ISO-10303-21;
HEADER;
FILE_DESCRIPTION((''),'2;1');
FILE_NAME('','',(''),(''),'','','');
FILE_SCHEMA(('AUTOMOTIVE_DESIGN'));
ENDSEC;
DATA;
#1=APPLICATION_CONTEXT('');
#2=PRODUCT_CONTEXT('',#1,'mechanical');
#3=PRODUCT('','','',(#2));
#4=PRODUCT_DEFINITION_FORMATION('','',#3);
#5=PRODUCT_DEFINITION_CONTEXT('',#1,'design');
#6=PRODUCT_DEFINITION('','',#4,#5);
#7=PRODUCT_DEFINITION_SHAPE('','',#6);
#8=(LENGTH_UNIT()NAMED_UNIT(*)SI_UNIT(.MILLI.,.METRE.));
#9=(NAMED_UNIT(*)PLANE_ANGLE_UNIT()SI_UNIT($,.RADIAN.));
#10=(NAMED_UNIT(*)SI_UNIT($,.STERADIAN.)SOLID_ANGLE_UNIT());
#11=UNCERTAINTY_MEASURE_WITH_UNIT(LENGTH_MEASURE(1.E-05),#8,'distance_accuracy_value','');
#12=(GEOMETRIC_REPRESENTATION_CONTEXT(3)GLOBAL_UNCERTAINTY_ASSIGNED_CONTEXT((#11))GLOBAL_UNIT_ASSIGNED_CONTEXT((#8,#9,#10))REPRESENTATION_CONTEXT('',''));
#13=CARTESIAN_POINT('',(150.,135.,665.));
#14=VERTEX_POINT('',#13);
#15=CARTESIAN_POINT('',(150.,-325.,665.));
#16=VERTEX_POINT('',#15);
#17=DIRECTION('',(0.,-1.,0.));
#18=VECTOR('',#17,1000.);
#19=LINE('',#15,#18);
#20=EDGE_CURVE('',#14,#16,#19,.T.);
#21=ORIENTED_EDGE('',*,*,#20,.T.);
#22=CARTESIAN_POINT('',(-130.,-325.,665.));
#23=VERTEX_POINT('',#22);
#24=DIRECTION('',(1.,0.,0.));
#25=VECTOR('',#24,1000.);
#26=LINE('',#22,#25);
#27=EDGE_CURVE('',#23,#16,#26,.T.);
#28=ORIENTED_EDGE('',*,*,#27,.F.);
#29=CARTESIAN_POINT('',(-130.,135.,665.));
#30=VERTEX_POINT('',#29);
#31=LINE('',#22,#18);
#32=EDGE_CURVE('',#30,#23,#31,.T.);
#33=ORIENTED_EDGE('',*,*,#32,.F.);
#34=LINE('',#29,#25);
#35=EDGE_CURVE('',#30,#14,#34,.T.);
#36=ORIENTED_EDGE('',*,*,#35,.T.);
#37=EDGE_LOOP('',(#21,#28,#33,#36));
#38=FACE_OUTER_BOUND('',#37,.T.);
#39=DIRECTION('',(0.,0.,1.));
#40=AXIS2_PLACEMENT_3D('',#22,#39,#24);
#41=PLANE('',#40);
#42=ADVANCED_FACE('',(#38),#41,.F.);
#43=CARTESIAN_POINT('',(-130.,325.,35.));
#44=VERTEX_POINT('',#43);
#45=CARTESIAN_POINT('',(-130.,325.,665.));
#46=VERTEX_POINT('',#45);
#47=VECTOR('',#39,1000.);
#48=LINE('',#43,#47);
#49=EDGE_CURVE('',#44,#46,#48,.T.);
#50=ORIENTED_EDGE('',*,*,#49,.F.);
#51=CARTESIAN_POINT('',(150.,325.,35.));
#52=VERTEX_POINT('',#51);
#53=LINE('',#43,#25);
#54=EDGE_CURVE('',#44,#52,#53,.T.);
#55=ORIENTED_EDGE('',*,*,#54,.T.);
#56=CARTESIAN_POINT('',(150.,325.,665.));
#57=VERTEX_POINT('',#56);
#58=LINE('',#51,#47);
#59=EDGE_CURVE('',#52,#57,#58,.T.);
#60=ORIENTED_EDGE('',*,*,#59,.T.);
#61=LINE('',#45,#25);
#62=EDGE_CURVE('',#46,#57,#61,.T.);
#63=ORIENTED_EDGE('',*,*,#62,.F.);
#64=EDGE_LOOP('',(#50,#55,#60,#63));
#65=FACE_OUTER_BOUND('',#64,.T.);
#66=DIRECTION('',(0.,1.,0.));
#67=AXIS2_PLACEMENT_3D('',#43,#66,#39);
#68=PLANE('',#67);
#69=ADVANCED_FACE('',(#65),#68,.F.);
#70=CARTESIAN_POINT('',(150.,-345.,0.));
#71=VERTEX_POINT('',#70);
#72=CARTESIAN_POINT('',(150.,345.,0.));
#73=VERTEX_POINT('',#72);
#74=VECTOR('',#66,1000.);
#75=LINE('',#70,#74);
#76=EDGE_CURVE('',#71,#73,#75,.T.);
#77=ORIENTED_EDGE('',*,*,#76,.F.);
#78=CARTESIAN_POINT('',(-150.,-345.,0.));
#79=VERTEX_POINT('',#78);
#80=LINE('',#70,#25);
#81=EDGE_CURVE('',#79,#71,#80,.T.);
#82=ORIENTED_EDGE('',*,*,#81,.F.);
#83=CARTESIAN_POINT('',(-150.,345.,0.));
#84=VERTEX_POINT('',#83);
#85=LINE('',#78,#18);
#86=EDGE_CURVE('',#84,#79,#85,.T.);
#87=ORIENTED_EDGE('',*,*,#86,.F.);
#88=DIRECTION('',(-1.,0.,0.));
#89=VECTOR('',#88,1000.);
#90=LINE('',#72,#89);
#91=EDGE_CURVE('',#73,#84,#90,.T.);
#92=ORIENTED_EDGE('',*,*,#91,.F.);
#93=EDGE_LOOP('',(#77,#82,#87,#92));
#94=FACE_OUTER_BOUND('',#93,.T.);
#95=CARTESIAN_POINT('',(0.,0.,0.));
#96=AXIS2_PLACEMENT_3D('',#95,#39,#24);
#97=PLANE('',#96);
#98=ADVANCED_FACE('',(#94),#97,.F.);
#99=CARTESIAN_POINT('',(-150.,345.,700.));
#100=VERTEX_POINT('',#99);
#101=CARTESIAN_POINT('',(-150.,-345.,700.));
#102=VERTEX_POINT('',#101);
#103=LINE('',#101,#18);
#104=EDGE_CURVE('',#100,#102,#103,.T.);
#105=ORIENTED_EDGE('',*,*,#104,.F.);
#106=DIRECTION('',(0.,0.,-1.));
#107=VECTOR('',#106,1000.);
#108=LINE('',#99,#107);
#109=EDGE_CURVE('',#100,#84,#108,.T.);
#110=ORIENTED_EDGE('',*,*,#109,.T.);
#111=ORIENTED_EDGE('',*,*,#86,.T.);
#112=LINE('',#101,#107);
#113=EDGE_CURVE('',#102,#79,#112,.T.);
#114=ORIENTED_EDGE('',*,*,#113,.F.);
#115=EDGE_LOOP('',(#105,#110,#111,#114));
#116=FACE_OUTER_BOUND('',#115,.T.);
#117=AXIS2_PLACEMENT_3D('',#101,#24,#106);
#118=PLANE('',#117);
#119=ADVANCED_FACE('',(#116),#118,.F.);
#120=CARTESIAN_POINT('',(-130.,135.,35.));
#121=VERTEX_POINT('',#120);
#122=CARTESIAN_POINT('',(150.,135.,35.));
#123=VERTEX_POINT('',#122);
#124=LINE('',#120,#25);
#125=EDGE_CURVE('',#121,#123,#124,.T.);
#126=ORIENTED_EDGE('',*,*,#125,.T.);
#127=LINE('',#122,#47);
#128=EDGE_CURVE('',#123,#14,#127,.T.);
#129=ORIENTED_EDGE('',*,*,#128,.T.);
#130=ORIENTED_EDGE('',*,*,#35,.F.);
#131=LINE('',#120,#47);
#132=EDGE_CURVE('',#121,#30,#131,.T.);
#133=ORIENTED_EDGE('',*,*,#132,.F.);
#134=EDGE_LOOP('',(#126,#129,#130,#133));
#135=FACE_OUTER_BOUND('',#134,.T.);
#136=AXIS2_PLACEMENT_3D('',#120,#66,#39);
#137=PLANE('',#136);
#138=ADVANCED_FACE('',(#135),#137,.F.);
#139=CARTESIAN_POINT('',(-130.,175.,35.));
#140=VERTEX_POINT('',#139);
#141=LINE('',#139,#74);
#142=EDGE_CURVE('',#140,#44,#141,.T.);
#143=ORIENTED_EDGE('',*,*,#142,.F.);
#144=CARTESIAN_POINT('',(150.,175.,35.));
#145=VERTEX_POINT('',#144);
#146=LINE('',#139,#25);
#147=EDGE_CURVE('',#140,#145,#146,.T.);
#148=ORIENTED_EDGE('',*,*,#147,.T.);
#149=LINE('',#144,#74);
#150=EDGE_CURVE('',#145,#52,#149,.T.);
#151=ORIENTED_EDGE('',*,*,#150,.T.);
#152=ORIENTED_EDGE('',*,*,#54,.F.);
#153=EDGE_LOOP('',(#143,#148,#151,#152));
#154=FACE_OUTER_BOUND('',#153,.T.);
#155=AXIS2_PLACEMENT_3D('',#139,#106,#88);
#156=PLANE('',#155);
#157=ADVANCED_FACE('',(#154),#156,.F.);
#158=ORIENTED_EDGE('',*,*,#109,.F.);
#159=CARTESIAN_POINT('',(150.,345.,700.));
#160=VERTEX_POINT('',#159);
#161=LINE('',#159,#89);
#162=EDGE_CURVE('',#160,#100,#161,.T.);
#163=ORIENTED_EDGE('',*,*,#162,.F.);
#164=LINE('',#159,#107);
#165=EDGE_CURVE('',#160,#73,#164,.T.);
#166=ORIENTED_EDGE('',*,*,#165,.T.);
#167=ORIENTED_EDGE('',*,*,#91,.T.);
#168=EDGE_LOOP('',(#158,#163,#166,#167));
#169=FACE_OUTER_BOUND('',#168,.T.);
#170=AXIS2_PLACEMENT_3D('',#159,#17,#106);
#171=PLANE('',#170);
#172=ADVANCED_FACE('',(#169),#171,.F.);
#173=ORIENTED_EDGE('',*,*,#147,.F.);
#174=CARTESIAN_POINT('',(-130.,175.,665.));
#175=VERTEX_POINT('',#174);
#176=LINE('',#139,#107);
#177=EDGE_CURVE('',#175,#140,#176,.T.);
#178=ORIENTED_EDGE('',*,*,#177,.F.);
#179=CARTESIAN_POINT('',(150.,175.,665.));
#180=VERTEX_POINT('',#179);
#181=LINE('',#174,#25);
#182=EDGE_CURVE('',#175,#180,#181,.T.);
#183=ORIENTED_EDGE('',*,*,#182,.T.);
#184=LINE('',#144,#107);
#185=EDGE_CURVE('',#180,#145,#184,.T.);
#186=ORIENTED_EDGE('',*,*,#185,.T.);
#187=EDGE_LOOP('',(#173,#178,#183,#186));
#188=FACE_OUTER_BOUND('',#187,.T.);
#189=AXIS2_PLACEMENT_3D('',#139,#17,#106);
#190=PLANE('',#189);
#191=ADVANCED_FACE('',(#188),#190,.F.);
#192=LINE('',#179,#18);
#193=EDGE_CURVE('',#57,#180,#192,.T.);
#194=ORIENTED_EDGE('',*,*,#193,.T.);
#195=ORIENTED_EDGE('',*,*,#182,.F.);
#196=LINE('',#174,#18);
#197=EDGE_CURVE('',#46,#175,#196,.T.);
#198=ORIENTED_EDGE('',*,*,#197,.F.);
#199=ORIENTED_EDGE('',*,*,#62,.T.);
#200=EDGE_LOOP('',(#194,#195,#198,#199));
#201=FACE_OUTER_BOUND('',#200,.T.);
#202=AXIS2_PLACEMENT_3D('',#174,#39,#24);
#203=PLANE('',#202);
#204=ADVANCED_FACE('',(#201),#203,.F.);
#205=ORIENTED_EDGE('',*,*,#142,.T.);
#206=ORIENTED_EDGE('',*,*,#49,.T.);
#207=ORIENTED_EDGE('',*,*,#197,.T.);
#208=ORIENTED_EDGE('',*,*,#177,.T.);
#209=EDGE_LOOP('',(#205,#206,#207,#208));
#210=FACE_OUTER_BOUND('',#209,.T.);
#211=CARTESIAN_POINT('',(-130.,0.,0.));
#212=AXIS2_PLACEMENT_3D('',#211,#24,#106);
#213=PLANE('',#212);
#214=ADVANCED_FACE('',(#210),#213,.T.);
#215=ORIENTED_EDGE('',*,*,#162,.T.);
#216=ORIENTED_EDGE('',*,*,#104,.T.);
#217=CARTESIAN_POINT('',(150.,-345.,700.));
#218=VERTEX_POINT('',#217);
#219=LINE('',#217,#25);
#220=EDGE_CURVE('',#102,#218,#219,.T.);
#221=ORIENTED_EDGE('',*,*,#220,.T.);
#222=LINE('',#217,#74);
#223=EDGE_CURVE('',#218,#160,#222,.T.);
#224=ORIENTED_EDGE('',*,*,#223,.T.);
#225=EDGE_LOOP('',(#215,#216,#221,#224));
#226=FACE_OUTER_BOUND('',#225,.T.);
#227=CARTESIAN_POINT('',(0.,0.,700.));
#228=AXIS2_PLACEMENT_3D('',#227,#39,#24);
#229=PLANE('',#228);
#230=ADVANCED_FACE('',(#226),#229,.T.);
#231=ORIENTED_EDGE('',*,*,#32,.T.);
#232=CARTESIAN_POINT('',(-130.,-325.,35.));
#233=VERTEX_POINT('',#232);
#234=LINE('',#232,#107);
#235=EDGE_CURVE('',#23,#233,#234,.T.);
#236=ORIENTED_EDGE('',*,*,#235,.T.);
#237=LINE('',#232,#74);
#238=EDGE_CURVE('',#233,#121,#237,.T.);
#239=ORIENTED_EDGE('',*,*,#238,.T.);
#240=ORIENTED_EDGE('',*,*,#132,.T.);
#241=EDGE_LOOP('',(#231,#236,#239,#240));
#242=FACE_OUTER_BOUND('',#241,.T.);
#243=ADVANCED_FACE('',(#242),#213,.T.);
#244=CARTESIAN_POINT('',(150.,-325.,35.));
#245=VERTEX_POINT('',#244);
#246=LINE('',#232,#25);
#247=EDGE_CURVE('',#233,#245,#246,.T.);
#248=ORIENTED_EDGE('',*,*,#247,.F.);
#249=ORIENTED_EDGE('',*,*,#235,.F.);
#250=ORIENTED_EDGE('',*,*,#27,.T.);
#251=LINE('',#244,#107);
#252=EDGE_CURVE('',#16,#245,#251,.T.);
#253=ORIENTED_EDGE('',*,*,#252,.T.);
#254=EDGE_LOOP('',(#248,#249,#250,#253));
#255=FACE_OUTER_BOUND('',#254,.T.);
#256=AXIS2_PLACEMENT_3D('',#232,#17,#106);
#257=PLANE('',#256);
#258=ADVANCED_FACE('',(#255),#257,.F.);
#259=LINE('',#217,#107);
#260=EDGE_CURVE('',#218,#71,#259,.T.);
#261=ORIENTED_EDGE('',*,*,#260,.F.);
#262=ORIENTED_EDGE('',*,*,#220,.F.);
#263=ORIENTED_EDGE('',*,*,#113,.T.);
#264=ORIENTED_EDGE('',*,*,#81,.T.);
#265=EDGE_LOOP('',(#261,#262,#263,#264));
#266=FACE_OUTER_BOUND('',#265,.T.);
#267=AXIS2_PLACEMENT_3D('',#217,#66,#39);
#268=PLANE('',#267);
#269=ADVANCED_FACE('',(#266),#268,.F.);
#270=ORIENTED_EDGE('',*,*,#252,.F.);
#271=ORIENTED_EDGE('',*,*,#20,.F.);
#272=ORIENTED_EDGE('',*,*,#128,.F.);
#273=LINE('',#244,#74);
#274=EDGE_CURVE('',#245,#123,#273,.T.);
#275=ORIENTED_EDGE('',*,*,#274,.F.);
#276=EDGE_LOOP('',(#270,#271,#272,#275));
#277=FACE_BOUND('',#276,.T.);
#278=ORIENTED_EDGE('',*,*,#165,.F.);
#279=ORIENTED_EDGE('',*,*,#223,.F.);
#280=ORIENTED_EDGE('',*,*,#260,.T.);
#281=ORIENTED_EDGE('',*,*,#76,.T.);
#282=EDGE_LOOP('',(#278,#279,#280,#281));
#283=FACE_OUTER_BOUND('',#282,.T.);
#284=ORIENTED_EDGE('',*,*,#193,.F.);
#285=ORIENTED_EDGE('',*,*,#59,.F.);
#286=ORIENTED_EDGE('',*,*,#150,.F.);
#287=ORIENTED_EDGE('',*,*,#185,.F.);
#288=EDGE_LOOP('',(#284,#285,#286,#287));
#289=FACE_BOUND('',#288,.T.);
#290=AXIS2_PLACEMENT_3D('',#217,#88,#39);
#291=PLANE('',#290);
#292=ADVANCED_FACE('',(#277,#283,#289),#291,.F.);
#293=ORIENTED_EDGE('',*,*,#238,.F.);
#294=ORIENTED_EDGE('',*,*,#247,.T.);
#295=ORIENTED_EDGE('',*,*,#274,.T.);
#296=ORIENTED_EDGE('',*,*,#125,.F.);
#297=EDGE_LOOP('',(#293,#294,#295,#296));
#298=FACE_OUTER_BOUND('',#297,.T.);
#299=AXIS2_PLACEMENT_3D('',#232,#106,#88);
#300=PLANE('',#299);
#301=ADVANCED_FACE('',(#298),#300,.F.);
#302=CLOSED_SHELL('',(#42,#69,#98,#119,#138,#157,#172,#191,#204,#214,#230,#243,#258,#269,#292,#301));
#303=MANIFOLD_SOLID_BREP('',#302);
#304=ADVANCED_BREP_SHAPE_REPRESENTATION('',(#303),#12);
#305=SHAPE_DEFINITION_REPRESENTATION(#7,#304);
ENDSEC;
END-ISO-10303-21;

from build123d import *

# Parameters (mm, degrees)
SKETCH1_W           = 300
SKETCH1_H           = 690
BOSS_EXTRUDE1_DEPTH = 700
SKETCH2_W           = 630
SKETCH2_H           = 150
CUT_EXTRUDE1_DEPTH  = 280
SKETCH3_W           = 630
SKETCH3_H           = 460
CUT_EXTRUDE2_DEPTH  = 280


with BuildPart() as part:
    # Sketch1 → Boss-Extrude1 (new body)
    with BuildSketch(Plane.XY):
        Rectangle(SKETCH1_W, SKETCH1_H)
    extrude(amount=BOSS_EXTRUDE1_DEPTH)

    # Sketch2 → Cut-Extrude1 (cut)
    with BuildSketch(Plane(origin=(150, 0, 0), x_dir=(0, 0, -1), z_dir=(1, 0, 0))):
        with Locations((-350, 250)):
            Rectangle(SKETCH2_W, SKETCH2_H)
    extrude(amount=-CUT_EXTRUDE1_DEPTH, mode=Mode.SUBTRACT)

    # Sketch3 → Cut-Extrude2 (cut)
    with BuildSketch(Plane(origin=(150, 0, 0), x_dir=(0, 0, -1), z_dir=(1, 0, 0))):
        with Locations((-350, -95)):
            Rectangle(SKETCH3_W, SKETCH3_H)
    extrude(amount=-CUT_EXTRUDE2_DEPTH, mode=Mode.SUBTRACT)


solid = part.part
